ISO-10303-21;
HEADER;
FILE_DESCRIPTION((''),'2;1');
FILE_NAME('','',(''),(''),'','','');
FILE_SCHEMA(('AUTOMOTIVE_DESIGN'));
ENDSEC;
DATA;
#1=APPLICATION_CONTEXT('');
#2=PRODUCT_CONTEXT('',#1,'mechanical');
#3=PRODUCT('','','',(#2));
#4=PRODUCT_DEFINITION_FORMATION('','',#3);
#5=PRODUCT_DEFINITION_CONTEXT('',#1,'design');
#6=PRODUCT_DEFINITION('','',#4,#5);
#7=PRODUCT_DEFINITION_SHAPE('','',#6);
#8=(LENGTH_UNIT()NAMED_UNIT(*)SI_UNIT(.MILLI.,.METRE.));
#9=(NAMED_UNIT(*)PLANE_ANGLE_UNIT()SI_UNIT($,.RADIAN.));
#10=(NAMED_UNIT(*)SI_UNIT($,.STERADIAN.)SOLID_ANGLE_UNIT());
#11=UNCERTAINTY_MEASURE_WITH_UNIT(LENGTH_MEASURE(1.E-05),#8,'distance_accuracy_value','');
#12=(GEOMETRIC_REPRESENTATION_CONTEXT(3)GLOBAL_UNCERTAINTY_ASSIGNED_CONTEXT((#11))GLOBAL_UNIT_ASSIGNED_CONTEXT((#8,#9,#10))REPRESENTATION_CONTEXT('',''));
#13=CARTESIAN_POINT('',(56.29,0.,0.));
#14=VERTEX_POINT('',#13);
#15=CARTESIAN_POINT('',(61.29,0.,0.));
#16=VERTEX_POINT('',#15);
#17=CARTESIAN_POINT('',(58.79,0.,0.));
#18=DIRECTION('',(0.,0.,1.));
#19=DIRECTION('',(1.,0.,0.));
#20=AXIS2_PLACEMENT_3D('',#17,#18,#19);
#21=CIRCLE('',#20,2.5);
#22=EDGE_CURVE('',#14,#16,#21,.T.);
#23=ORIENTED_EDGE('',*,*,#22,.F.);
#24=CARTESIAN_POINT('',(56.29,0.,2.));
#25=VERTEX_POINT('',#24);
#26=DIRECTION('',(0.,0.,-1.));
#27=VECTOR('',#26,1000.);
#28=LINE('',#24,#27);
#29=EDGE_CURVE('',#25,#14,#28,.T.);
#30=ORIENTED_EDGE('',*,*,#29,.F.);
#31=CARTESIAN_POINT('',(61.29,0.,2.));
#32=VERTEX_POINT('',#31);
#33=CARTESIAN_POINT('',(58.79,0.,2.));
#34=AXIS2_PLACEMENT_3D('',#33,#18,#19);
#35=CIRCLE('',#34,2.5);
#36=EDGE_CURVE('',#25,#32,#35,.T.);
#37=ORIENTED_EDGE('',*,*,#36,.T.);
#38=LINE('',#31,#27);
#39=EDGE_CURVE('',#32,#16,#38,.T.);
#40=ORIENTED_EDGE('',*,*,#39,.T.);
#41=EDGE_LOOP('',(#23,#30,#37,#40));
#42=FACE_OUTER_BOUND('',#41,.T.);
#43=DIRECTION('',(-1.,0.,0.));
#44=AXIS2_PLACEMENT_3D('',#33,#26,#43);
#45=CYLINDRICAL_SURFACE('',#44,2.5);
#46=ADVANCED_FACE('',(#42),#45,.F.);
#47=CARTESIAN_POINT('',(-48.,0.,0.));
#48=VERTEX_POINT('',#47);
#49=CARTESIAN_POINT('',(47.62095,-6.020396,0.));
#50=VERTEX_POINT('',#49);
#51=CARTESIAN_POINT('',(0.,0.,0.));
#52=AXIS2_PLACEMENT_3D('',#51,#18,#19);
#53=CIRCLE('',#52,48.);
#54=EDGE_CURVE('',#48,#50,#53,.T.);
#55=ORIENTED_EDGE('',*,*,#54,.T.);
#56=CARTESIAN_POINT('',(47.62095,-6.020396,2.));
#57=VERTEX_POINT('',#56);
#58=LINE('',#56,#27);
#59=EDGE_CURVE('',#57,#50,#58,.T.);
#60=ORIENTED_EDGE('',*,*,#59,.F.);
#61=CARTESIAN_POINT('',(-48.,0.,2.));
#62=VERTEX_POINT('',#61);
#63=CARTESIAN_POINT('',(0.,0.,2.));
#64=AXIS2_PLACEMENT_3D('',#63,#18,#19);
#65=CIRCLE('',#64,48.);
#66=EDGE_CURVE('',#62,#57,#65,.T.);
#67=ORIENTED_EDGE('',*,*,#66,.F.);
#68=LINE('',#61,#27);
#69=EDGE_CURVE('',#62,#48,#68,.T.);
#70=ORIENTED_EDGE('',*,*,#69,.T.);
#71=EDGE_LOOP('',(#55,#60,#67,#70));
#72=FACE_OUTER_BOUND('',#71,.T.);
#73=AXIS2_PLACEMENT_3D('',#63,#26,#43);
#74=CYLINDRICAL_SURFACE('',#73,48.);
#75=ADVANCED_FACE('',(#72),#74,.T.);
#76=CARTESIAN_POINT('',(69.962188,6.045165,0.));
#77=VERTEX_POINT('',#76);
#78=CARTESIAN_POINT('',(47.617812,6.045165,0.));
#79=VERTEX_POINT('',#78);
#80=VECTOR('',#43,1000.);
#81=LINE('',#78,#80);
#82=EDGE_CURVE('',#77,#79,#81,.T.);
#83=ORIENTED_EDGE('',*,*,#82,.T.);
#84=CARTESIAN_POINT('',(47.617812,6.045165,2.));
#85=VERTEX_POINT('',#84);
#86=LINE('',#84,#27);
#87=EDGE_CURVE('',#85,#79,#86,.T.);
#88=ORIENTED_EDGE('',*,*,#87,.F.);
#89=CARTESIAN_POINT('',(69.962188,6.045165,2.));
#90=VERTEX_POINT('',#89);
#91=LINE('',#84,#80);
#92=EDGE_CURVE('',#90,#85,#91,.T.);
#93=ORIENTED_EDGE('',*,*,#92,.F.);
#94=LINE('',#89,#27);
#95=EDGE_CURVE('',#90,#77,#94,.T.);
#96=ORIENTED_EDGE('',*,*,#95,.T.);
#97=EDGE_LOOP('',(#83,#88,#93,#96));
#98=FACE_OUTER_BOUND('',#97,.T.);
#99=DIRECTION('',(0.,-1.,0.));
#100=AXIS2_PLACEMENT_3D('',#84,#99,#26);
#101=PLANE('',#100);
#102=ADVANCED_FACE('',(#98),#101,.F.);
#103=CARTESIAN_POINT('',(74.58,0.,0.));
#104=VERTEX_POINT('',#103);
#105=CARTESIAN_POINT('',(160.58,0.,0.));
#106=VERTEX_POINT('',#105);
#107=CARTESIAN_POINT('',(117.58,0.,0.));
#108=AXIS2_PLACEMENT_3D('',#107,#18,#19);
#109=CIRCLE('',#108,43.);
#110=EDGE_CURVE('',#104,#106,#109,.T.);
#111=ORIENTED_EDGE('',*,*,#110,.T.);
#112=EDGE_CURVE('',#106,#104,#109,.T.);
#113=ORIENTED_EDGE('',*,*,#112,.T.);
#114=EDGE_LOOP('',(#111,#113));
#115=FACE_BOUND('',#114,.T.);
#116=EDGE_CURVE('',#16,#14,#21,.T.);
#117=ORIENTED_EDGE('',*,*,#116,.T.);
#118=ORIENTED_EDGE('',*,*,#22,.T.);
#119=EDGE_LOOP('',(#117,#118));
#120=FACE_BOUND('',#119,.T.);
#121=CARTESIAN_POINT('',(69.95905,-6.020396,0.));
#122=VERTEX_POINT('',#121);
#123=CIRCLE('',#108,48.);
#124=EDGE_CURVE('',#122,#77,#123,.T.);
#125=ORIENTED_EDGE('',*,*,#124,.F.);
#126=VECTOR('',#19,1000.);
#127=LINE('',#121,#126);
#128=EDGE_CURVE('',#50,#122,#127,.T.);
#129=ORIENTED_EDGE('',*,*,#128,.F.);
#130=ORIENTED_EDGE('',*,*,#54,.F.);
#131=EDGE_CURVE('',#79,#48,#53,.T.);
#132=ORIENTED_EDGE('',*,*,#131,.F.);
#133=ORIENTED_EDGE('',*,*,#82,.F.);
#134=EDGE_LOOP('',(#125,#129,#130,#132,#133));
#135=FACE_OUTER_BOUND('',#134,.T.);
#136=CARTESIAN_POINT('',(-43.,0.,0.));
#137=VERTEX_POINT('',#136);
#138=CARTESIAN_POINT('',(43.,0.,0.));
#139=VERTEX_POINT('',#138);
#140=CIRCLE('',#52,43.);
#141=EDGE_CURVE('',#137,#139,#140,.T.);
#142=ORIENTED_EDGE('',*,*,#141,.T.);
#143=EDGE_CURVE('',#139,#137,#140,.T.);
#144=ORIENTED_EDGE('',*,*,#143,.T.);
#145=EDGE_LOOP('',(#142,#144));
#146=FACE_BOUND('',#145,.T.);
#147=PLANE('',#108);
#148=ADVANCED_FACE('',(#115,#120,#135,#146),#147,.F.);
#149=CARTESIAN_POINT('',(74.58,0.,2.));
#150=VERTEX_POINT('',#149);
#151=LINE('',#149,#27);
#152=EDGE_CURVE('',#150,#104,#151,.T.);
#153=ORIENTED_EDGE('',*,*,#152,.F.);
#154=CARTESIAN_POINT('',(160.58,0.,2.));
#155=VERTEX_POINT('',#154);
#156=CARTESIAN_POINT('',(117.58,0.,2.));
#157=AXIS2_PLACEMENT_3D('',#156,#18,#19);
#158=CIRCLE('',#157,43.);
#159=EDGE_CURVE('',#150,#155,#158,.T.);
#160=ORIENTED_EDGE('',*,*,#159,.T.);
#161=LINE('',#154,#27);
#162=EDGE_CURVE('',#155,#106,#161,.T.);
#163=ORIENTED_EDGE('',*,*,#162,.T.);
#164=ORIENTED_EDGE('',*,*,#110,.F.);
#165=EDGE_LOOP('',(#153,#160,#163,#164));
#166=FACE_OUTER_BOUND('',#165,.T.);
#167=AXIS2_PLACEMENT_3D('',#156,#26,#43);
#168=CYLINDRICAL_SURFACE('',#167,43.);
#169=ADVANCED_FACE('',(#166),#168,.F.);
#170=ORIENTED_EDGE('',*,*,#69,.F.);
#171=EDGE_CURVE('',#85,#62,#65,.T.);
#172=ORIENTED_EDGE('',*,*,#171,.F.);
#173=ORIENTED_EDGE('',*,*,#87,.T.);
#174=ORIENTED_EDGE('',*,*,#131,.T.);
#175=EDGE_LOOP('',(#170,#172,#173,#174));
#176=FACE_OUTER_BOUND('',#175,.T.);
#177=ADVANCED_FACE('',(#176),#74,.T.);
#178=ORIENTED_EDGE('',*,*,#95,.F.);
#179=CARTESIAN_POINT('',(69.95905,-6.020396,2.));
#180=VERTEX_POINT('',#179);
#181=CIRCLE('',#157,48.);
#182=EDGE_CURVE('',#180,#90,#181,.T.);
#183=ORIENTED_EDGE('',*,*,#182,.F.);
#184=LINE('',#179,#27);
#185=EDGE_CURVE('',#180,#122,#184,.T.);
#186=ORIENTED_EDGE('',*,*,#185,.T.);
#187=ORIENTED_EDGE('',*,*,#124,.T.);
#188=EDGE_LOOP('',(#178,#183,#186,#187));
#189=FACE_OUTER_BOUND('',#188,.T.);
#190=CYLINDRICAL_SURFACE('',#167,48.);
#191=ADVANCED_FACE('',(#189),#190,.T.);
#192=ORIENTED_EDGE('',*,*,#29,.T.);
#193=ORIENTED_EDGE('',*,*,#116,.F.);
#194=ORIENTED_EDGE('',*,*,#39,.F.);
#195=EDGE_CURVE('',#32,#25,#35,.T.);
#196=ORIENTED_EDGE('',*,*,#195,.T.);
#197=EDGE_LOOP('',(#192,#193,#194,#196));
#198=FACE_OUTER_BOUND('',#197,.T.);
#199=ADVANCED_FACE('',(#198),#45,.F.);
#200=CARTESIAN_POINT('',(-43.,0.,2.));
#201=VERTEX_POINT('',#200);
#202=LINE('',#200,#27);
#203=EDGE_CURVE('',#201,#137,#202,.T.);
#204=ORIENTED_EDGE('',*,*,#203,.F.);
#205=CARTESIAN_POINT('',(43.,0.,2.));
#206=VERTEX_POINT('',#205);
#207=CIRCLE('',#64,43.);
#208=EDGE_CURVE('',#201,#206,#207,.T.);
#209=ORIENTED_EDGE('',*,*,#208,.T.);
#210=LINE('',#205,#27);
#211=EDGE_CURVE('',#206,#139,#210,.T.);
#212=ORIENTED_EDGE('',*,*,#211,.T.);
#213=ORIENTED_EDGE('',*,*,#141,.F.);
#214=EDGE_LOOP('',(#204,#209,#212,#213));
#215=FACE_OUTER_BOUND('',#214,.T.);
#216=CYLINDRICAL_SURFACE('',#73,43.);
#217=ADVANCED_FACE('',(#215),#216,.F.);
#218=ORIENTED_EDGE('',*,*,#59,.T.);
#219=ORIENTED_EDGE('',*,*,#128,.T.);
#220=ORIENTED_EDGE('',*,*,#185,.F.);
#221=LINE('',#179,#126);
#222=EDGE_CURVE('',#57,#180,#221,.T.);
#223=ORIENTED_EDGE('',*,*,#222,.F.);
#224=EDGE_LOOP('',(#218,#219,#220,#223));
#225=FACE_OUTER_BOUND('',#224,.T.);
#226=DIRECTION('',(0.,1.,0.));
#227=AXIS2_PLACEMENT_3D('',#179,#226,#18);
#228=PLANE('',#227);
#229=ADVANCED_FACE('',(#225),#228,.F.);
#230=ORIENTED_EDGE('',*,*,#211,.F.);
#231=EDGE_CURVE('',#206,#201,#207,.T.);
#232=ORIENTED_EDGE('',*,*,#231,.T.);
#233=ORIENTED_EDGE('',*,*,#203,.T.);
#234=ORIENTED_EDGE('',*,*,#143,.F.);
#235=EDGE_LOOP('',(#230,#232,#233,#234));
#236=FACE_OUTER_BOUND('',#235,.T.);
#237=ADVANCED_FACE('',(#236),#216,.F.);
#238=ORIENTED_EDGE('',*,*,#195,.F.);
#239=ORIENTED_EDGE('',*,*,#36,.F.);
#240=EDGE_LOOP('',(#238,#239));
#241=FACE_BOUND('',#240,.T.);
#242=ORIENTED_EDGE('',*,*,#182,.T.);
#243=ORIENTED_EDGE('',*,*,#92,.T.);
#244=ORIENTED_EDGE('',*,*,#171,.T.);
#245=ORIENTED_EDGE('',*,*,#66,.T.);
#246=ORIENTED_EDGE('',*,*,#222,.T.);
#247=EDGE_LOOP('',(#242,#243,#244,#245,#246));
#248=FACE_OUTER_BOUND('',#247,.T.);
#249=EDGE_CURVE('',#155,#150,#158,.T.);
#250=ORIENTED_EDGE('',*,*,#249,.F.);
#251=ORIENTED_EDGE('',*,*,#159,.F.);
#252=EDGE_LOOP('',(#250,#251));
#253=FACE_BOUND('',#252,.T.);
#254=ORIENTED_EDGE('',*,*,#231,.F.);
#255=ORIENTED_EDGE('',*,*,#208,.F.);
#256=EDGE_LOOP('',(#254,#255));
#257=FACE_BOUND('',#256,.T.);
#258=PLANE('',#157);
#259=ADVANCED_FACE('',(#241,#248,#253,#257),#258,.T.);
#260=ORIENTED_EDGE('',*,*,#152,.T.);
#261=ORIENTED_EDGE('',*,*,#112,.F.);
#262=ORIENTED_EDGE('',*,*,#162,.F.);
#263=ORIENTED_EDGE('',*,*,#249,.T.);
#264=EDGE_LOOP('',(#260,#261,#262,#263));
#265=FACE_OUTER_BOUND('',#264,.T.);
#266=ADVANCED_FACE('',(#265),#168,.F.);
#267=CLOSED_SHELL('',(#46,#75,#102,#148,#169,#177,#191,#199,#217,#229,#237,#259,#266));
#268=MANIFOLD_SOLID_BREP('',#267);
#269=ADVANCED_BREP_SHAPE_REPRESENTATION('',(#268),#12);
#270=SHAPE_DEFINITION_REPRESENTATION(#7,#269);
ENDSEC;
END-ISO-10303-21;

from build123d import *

# Parameters (mm, degrees)
SKETCH1_R           = 43
SKETCH1_R_2         = 2.5
BOSS_EXTRUDE1_DEPTH = 2


with BuildPart() as part:
    # Sketch1 → Boss-Extrude1 (new body)
    with BuildSketch(Plane.XY):
        with BuildLine():
            Line((47.617811618, 6.045164742), (69.962188382, 6.045164742))
            ThreePointArc((69.962188382, 6.045164742), (165.579998377, -0.012483332), (69.959050499, -6.020396052))
            Line((69.959050499, -6.020396052), (47.620949501, -6.020396052))
            ThreePointArc((47.620949501, -6.020396052), (-47.999998377, -0.012483332), (47.617811618, 6.045164742))
        make_face()
        Circle(SKETCH1_R, mode=Mode.SUBTRACT)
        with Locations((117.58, 0)):
            Circle(SKETCH1_R, mode=Mode.SUBTRACT)
        with Locations((58.79, 0)):
            Circle(SKETCH1_R_2, mode=Mode.SUBTRACT)
    extrude(amount=BOSS_EXTRUDE1_DEPTH)


solid = part.part
